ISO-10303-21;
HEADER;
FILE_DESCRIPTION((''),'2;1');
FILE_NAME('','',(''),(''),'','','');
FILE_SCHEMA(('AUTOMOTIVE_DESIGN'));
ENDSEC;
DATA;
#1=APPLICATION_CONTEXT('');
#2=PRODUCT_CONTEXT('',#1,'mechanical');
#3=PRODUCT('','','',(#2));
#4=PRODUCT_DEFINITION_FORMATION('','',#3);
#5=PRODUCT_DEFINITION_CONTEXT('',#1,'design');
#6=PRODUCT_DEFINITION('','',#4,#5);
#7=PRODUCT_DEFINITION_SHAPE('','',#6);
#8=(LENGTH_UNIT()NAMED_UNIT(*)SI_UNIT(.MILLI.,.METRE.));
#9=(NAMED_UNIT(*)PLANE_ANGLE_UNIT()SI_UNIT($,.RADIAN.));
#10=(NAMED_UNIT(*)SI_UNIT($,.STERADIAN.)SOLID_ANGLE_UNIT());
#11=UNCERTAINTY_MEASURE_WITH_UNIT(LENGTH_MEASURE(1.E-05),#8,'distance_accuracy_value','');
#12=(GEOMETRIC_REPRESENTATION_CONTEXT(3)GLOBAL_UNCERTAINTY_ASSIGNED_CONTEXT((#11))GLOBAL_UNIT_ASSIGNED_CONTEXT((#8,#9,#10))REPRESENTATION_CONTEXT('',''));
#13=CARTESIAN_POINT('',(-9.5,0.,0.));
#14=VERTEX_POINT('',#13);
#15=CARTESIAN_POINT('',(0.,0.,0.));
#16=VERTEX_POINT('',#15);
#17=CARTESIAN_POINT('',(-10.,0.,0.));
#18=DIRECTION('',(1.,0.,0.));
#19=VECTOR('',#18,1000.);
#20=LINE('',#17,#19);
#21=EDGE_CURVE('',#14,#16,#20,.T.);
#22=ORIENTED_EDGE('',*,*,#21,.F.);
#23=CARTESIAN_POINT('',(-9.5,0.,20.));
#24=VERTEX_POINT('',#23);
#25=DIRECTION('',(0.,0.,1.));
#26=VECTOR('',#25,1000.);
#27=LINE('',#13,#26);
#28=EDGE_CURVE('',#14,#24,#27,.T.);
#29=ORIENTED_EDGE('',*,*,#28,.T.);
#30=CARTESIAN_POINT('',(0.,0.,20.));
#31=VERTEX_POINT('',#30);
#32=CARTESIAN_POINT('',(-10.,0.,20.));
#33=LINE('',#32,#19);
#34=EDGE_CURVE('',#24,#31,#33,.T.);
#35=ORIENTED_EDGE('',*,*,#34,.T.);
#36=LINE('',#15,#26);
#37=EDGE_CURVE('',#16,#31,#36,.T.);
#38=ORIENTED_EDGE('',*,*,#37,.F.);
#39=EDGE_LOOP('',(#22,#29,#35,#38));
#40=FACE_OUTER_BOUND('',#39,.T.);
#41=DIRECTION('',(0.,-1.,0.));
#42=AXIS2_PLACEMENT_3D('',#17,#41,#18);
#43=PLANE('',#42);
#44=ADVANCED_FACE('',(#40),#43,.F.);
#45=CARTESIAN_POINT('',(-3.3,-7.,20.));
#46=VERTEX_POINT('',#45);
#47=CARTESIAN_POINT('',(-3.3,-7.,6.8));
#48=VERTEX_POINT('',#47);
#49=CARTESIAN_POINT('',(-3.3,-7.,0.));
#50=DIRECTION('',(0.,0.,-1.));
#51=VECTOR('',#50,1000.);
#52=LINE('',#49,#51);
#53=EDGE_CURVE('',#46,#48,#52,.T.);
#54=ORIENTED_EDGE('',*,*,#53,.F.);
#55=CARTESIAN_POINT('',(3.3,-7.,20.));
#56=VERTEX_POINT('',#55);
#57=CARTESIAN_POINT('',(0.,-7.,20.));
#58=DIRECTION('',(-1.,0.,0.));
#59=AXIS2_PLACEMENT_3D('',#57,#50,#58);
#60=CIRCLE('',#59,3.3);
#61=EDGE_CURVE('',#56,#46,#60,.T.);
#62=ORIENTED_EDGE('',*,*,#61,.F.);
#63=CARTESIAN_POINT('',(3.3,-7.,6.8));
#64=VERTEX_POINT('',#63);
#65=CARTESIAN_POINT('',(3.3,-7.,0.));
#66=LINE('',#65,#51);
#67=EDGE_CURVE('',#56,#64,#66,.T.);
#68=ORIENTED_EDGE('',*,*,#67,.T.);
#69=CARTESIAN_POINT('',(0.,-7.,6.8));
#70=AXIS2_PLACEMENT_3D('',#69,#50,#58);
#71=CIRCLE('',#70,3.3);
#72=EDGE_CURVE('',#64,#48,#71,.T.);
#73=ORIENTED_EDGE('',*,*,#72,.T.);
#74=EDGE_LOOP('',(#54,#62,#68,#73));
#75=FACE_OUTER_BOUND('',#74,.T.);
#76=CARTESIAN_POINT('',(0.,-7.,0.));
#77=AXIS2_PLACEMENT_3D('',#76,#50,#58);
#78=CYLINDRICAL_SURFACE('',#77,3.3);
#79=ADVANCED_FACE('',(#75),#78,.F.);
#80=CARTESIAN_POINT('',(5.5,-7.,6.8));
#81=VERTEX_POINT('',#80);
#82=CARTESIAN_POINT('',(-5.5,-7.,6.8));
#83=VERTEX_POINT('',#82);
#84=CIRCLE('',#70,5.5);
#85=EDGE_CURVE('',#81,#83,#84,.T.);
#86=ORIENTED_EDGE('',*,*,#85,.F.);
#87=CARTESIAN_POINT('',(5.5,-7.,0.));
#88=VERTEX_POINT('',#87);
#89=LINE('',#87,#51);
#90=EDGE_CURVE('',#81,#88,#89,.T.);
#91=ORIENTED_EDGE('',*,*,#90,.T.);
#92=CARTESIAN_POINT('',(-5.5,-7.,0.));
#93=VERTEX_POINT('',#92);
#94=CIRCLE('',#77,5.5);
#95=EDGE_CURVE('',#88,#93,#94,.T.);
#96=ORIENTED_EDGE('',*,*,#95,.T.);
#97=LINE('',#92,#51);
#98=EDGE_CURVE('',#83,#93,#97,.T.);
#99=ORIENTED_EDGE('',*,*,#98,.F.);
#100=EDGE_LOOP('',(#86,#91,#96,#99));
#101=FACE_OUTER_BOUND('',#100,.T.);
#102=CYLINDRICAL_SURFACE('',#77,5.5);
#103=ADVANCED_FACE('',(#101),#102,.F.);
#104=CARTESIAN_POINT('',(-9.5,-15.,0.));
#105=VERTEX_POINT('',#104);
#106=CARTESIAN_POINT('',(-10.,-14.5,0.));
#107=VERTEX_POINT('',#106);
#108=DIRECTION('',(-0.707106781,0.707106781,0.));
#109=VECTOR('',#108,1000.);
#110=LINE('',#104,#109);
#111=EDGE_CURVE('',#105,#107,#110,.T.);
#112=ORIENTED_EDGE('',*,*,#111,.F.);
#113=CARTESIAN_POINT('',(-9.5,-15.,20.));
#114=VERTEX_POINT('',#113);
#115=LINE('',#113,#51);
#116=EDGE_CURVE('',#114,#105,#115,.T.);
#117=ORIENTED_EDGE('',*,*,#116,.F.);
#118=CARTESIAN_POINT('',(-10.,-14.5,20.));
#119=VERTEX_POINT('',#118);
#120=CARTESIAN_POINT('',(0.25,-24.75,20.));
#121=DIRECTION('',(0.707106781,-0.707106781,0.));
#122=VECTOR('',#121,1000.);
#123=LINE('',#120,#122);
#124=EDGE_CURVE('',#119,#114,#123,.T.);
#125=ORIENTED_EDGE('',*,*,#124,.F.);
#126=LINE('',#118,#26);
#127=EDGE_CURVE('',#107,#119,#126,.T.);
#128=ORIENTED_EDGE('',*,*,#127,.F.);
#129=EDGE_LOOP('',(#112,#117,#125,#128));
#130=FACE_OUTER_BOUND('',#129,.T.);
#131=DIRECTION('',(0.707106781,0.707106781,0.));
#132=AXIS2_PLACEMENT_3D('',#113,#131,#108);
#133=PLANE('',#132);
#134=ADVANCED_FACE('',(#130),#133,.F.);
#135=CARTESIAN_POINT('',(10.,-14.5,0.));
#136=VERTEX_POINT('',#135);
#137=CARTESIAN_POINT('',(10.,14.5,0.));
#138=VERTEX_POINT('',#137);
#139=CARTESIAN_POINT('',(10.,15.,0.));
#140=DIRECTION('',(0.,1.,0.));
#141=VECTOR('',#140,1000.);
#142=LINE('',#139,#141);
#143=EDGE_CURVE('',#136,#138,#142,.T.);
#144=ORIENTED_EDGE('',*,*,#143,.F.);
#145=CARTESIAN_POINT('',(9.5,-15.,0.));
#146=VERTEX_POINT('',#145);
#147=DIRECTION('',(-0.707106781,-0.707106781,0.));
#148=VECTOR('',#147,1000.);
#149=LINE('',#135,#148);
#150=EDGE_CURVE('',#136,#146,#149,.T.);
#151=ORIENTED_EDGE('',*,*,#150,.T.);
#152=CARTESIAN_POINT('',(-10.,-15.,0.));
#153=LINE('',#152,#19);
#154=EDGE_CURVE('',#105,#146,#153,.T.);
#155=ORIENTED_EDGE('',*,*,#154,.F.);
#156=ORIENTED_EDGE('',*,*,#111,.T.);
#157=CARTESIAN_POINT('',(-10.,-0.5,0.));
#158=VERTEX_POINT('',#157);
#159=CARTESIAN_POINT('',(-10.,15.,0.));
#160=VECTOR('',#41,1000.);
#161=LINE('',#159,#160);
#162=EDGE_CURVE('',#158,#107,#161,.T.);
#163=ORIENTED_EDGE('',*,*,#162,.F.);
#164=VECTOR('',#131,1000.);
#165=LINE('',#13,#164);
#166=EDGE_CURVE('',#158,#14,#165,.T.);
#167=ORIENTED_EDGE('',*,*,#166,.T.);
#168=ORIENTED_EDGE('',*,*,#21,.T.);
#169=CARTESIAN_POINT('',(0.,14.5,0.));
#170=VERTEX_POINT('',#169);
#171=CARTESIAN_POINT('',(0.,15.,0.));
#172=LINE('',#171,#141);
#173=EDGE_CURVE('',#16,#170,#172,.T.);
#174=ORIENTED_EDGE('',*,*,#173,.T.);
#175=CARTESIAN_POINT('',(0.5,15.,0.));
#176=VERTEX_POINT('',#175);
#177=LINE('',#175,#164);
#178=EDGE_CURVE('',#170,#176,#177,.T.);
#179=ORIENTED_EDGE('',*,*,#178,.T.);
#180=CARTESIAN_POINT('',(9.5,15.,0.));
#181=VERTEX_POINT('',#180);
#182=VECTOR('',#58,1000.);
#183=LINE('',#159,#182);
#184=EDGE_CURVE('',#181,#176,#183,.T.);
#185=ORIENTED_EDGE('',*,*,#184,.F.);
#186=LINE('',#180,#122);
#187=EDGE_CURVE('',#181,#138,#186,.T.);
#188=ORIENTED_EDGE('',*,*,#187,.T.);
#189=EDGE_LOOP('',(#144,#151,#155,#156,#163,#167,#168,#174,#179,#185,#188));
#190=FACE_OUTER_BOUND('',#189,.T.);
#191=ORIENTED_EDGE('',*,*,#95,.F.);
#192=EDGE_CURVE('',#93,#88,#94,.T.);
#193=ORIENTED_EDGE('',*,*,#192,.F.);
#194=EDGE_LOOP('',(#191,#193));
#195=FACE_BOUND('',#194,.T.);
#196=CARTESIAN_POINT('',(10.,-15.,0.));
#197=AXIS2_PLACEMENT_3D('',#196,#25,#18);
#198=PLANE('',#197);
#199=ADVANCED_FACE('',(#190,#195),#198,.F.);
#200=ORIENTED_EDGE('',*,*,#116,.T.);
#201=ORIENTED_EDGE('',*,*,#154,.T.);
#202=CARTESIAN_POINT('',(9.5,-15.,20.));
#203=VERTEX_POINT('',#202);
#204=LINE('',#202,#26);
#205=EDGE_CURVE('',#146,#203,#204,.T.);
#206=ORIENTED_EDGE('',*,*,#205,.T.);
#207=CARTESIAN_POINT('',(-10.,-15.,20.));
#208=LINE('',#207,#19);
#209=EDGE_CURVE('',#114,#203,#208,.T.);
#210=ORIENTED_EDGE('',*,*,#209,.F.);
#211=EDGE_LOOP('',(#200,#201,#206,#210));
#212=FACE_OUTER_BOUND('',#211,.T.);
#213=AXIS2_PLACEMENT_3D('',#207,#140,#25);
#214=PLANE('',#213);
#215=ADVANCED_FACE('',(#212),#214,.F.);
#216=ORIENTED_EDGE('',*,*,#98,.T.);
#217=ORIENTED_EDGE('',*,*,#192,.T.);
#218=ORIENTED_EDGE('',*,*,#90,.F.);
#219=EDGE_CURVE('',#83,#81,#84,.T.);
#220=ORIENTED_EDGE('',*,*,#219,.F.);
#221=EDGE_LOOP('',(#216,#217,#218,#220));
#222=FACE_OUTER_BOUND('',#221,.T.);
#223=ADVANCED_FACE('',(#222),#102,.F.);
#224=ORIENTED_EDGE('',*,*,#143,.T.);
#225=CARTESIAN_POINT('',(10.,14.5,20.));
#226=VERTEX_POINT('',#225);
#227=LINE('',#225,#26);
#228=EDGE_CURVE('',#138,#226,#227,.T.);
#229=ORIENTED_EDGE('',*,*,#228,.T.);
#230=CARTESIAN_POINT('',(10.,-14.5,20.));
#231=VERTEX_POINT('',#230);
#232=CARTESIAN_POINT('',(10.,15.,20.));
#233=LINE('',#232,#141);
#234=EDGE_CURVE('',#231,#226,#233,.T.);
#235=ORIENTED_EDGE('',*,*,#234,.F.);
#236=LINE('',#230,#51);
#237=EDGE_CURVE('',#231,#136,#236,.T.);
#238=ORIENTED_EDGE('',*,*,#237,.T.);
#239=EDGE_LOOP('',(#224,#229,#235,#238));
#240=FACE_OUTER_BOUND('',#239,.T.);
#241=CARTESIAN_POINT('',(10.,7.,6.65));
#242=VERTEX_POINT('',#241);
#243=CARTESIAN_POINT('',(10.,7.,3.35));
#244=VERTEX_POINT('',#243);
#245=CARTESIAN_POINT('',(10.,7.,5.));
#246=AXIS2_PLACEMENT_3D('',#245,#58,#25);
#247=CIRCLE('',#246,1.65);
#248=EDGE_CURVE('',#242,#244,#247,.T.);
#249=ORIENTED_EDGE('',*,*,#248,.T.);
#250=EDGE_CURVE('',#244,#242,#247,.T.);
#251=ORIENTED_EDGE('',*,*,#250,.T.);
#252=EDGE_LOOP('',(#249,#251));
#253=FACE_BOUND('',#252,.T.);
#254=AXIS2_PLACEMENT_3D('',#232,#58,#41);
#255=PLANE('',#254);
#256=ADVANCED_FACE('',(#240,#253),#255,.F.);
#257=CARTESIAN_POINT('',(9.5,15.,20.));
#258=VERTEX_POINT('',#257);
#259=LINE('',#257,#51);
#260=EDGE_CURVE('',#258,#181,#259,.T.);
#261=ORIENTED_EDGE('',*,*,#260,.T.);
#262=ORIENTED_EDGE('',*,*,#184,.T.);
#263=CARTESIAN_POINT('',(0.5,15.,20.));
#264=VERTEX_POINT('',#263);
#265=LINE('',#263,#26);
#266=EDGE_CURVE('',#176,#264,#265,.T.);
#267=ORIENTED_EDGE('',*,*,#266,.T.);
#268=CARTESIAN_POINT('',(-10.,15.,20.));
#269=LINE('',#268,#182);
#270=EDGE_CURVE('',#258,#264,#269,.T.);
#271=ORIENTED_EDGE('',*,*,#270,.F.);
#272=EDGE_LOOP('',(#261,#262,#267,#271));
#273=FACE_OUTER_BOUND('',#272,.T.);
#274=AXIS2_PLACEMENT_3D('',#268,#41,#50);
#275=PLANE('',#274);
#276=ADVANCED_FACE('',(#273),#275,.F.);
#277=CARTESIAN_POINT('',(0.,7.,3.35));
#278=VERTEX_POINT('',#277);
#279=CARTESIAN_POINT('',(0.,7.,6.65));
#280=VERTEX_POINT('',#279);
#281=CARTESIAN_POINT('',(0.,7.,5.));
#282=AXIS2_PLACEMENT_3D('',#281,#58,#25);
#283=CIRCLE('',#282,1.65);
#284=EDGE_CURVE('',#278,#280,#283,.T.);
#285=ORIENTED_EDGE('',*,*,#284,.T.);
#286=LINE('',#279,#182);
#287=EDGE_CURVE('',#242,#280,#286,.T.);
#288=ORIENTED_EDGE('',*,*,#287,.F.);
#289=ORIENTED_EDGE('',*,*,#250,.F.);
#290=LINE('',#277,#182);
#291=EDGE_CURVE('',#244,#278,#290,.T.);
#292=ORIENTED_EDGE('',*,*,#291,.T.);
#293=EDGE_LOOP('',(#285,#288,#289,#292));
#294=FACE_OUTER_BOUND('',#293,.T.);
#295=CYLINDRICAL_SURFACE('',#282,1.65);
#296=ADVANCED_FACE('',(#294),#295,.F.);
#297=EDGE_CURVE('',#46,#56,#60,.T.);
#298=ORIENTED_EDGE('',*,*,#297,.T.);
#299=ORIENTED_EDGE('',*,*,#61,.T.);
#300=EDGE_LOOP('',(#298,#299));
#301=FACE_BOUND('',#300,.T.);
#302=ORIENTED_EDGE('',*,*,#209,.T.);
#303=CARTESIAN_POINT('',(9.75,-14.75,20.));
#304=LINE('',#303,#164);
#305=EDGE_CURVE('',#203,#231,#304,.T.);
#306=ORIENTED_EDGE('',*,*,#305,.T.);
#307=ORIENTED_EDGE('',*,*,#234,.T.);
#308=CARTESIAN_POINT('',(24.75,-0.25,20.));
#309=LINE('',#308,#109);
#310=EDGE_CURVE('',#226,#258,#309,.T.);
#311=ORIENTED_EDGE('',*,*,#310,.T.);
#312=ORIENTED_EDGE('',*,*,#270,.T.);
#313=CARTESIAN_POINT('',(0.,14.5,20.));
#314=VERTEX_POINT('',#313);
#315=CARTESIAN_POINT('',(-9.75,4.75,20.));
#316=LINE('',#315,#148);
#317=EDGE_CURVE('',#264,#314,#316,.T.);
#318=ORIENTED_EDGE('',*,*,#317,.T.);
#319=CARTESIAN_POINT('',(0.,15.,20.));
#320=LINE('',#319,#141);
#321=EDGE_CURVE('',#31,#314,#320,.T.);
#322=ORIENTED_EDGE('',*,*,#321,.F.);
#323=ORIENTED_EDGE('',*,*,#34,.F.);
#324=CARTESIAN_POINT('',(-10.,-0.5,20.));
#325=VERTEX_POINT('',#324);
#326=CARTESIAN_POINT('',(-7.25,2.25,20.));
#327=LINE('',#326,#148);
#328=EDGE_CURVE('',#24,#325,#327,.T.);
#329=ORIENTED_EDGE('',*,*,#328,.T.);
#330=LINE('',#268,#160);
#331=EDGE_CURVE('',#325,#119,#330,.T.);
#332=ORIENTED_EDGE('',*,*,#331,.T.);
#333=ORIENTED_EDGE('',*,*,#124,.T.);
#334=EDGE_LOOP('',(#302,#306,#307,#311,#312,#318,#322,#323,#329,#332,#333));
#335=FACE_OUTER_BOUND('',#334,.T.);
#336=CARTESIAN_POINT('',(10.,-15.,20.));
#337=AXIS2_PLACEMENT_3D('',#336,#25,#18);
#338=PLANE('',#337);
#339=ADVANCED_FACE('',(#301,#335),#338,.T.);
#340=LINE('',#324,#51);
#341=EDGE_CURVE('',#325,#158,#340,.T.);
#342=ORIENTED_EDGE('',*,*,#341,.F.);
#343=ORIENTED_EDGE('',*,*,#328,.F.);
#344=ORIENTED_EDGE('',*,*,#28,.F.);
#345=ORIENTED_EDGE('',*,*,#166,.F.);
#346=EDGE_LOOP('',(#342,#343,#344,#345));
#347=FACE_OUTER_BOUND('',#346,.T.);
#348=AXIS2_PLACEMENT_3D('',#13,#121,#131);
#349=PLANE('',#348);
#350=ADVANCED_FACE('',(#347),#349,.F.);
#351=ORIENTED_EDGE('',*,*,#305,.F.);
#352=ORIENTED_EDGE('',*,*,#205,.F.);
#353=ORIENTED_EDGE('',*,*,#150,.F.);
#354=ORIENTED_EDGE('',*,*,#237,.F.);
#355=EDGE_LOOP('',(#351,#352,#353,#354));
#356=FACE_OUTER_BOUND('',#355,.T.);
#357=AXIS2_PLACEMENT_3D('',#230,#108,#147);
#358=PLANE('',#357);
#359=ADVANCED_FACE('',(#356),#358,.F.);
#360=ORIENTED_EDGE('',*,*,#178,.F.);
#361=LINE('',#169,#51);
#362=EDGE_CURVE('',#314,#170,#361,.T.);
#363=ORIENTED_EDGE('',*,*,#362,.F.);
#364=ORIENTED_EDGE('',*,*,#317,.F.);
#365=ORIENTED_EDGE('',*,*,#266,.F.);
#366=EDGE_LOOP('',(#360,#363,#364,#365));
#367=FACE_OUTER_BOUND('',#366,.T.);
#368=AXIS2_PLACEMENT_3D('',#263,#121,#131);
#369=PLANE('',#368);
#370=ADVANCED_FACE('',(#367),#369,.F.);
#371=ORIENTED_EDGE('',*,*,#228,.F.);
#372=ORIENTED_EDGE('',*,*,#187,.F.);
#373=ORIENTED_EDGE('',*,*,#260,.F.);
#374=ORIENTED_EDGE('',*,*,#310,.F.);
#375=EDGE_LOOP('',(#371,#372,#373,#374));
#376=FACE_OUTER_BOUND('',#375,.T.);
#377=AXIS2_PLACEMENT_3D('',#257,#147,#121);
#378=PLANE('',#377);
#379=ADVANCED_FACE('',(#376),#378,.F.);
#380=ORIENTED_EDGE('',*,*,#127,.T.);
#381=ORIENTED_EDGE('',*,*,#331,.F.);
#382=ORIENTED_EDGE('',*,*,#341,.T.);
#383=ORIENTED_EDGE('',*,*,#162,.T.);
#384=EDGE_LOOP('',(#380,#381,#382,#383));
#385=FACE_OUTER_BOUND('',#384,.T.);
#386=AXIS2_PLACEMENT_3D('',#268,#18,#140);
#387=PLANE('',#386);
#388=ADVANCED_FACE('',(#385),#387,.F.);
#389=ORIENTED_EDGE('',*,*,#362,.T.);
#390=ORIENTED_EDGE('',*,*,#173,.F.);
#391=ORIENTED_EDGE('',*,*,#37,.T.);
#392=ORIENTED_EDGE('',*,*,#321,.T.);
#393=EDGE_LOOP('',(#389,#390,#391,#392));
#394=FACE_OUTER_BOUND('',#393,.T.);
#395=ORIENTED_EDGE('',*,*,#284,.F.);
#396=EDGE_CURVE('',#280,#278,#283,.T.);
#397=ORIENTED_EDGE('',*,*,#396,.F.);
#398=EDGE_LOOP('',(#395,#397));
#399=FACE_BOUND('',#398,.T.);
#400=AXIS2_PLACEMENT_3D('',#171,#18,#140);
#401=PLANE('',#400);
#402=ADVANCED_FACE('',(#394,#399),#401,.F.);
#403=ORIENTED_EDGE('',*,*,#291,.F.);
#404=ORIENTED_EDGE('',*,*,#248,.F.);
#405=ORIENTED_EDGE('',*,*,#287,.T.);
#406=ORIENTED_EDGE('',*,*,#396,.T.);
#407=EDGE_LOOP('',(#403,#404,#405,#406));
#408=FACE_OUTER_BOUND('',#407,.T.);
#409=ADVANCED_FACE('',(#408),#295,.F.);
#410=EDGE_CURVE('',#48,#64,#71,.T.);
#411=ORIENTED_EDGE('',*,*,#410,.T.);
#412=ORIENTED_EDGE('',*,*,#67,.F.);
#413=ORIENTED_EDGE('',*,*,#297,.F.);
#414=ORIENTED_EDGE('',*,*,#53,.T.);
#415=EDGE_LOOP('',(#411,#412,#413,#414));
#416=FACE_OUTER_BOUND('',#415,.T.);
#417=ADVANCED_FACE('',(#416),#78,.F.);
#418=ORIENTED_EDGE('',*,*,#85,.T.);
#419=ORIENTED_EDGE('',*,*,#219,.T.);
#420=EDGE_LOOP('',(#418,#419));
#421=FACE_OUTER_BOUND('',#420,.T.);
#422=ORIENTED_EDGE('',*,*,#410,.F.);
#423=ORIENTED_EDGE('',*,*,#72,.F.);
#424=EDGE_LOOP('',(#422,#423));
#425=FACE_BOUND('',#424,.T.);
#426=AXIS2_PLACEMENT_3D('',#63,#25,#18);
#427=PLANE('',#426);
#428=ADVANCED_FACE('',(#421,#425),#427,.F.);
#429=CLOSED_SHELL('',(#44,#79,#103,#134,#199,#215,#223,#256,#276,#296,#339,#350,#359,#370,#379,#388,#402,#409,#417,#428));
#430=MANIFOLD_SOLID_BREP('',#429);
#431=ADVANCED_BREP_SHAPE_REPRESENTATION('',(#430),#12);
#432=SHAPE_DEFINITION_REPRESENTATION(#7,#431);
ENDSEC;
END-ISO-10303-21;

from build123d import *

# Parameters (mm, degrees)
SKETCH_1_W                = 20
SKETCH_1_H                = 30
EXTRUDE_1_DEPTH           = 20
HOLE_WIZARD_1_D           = 6.6
HOLE_WIZARD_1_CBORE_D     = 11
HOLE_WIZARD_1_CBORE_DEPTH = 6.8
SKETCH_4_W                = 10
SKETCH_4_H                = 15
CUT_EXTRUDE_1_DEPTH       = 27.925824036
HOLE_WIZARD_M4_1_D        = 3.3
CHAMFER_1_SIZE            = 0.5


with BuildPart() as part:
    # 草图1 → 凸台-拉伸1 (new body)
    with BuildSketch(Plane.XY):
        Rectangle(SKETCH_1_W, SKETCH_1_H)
    extrude(amount=EXTRUDE_1_DEPTH)

    # 打孔尺寸根据内六角圆柱头螺钉的类型1 (through all)
    with Locations(Plane(origin=(3.133596483, 10.907898158, 0), x_dir=(1, 0, 0), z_dir=(0, 0, -1))):
        with Locations((-3.133596483, 17.907898158)):
            CounterBoreHole(HOLE_WIZARD_1_D / 2, HOLE_WIZARD_1_CBORE_D / 2, HOLE_WIZARD_1_CBORE_DEPTH)

    # 草图4 → 切除-拉伸1 (cut, through all)
    with BuildSketch(Plane.XY.offset(20)):
        with Locations((-5, 7.5)):
            Rectangle(SKETCH_4_W, SKETCH_4_H)
    extrude(amount=-CUT_EXTRUDE_1_DEPTH, mode=Mode.SUBTRACT)

    # M4 螺纹孔1 (through all)
    with Locations(Plane.ZY):
        with Locations((5, 7)):
            Hole(HOLE_WIZARD_M4_1_D / 2)

    # 倒角1
    chamfer_1_edges = [part.edges().sort_by_distance(p)[0] for p in [
        (-10, 0, 10),
        (0, 15, 10),
        (10, -15, 10),
        (-10, -15, 10),
        (10, 15, 10),
    ]]
    chamfer(chamfer_1_edges, length=CHAMFER_1_SIZE)


solid = part.part
